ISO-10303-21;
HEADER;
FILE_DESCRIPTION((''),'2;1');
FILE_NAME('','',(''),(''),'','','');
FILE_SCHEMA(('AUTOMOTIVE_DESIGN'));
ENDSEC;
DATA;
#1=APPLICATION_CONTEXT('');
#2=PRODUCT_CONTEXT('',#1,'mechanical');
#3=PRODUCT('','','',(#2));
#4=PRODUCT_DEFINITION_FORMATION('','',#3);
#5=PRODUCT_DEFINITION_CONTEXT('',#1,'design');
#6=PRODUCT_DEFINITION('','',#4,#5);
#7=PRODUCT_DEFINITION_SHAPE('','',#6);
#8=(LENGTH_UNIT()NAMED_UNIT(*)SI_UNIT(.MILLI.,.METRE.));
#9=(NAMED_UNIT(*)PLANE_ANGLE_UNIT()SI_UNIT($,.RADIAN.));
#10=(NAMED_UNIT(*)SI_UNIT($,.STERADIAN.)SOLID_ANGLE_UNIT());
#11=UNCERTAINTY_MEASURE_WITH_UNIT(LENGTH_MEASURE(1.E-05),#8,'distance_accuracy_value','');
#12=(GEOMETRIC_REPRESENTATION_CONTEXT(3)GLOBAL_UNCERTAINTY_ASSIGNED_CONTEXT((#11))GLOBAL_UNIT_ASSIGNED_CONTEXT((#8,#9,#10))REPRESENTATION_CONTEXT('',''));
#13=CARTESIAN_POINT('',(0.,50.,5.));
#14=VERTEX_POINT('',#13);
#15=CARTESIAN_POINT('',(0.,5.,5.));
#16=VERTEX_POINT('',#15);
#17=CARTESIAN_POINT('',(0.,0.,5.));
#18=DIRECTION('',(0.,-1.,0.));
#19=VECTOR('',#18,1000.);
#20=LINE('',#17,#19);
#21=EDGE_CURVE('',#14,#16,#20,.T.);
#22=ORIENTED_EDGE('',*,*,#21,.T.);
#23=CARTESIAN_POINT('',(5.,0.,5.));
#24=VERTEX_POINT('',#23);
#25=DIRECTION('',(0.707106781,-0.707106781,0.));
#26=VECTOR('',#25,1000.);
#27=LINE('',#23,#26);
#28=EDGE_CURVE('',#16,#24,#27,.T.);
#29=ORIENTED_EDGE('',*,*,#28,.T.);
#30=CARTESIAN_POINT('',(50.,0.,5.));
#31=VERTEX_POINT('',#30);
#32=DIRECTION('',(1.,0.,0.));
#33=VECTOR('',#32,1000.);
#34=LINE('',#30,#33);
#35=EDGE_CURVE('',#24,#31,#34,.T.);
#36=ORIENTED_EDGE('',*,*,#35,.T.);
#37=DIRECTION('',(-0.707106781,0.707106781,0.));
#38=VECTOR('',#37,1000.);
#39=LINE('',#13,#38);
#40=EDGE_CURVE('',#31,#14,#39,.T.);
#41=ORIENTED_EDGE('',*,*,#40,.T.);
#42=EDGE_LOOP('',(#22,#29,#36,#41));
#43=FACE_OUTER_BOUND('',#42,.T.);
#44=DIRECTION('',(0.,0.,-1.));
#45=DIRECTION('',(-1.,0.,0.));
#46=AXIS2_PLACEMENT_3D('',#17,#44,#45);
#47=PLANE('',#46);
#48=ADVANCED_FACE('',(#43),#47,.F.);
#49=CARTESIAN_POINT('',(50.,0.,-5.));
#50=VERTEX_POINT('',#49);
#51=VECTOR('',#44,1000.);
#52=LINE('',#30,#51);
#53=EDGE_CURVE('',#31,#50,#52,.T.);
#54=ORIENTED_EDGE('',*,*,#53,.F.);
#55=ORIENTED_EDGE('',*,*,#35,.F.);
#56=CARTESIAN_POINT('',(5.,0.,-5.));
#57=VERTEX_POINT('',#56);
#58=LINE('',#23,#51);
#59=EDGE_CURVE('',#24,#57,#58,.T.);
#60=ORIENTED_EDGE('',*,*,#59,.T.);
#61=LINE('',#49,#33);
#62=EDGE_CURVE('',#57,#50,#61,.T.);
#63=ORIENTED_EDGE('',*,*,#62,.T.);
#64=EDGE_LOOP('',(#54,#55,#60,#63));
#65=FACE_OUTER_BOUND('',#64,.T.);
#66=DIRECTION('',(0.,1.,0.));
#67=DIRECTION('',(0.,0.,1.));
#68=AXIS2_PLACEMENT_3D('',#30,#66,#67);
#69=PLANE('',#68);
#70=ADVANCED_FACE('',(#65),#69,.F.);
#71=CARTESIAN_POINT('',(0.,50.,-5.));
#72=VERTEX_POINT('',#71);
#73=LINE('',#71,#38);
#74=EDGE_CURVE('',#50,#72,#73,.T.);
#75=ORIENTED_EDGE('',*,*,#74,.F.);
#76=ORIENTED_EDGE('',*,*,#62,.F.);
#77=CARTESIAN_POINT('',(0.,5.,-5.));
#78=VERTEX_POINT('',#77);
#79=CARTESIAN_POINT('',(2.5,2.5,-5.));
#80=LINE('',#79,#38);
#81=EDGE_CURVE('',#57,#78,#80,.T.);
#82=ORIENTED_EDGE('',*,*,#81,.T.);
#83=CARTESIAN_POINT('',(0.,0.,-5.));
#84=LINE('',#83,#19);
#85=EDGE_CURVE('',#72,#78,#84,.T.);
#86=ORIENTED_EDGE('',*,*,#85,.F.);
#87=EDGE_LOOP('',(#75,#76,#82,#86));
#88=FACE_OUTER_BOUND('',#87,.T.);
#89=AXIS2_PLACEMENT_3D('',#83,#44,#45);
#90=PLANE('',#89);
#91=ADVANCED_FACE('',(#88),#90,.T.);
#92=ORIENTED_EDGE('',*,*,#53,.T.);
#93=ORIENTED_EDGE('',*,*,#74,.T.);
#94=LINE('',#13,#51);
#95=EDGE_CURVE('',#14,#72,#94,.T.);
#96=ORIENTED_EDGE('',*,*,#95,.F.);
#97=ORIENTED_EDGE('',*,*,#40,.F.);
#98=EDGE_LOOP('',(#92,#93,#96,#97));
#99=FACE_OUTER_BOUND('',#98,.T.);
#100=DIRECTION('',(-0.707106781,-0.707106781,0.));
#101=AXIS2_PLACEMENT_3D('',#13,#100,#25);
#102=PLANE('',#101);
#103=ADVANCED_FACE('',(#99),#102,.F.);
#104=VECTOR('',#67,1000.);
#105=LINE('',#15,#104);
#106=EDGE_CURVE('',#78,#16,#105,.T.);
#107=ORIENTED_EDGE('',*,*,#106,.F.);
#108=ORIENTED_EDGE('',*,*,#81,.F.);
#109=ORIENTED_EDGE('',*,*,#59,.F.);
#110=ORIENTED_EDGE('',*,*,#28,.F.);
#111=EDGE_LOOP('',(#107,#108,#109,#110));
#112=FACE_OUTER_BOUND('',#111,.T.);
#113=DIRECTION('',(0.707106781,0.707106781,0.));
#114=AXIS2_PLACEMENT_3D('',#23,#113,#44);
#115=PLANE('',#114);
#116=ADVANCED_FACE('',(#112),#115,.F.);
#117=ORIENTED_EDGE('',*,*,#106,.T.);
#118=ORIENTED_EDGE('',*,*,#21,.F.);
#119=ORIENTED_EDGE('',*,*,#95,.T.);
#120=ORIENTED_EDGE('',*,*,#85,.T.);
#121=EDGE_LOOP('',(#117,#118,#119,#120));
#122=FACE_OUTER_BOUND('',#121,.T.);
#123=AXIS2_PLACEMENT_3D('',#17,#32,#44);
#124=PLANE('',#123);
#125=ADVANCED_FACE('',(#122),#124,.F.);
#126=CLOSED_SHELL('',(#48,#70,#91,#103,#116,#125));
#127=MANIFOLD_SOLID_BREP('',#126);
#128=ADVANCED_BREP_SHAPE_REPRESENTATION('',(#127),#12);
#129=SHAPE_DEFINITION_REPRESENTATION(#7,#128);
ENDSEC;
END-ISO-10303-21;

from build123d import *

# Parameters (mm, degrees)
BOSS_EXTRUDE1_DEPTH = 5
CHAMFER1_SIZE       = 5


with BuildPart() as part:
    # Sketch1 → Boss-Extrude1 (new, symmetric)
    with BuildSketch(Plane.XY):
        Polygon((0, 0), (0, 50), (50, 0), align=None)
    extrude(amount=BOSS_EXTRUDE1_DEPTH, both=True)

    # Chamfer1
    chamfer1_edges = [part.edges().sort_by_distance(p)[0] for p in [
        (0, 0, 0),
    ]]
    chamfer(chamfer1_edges, length=CHAMFER1_SIZE)


solid = part.part
